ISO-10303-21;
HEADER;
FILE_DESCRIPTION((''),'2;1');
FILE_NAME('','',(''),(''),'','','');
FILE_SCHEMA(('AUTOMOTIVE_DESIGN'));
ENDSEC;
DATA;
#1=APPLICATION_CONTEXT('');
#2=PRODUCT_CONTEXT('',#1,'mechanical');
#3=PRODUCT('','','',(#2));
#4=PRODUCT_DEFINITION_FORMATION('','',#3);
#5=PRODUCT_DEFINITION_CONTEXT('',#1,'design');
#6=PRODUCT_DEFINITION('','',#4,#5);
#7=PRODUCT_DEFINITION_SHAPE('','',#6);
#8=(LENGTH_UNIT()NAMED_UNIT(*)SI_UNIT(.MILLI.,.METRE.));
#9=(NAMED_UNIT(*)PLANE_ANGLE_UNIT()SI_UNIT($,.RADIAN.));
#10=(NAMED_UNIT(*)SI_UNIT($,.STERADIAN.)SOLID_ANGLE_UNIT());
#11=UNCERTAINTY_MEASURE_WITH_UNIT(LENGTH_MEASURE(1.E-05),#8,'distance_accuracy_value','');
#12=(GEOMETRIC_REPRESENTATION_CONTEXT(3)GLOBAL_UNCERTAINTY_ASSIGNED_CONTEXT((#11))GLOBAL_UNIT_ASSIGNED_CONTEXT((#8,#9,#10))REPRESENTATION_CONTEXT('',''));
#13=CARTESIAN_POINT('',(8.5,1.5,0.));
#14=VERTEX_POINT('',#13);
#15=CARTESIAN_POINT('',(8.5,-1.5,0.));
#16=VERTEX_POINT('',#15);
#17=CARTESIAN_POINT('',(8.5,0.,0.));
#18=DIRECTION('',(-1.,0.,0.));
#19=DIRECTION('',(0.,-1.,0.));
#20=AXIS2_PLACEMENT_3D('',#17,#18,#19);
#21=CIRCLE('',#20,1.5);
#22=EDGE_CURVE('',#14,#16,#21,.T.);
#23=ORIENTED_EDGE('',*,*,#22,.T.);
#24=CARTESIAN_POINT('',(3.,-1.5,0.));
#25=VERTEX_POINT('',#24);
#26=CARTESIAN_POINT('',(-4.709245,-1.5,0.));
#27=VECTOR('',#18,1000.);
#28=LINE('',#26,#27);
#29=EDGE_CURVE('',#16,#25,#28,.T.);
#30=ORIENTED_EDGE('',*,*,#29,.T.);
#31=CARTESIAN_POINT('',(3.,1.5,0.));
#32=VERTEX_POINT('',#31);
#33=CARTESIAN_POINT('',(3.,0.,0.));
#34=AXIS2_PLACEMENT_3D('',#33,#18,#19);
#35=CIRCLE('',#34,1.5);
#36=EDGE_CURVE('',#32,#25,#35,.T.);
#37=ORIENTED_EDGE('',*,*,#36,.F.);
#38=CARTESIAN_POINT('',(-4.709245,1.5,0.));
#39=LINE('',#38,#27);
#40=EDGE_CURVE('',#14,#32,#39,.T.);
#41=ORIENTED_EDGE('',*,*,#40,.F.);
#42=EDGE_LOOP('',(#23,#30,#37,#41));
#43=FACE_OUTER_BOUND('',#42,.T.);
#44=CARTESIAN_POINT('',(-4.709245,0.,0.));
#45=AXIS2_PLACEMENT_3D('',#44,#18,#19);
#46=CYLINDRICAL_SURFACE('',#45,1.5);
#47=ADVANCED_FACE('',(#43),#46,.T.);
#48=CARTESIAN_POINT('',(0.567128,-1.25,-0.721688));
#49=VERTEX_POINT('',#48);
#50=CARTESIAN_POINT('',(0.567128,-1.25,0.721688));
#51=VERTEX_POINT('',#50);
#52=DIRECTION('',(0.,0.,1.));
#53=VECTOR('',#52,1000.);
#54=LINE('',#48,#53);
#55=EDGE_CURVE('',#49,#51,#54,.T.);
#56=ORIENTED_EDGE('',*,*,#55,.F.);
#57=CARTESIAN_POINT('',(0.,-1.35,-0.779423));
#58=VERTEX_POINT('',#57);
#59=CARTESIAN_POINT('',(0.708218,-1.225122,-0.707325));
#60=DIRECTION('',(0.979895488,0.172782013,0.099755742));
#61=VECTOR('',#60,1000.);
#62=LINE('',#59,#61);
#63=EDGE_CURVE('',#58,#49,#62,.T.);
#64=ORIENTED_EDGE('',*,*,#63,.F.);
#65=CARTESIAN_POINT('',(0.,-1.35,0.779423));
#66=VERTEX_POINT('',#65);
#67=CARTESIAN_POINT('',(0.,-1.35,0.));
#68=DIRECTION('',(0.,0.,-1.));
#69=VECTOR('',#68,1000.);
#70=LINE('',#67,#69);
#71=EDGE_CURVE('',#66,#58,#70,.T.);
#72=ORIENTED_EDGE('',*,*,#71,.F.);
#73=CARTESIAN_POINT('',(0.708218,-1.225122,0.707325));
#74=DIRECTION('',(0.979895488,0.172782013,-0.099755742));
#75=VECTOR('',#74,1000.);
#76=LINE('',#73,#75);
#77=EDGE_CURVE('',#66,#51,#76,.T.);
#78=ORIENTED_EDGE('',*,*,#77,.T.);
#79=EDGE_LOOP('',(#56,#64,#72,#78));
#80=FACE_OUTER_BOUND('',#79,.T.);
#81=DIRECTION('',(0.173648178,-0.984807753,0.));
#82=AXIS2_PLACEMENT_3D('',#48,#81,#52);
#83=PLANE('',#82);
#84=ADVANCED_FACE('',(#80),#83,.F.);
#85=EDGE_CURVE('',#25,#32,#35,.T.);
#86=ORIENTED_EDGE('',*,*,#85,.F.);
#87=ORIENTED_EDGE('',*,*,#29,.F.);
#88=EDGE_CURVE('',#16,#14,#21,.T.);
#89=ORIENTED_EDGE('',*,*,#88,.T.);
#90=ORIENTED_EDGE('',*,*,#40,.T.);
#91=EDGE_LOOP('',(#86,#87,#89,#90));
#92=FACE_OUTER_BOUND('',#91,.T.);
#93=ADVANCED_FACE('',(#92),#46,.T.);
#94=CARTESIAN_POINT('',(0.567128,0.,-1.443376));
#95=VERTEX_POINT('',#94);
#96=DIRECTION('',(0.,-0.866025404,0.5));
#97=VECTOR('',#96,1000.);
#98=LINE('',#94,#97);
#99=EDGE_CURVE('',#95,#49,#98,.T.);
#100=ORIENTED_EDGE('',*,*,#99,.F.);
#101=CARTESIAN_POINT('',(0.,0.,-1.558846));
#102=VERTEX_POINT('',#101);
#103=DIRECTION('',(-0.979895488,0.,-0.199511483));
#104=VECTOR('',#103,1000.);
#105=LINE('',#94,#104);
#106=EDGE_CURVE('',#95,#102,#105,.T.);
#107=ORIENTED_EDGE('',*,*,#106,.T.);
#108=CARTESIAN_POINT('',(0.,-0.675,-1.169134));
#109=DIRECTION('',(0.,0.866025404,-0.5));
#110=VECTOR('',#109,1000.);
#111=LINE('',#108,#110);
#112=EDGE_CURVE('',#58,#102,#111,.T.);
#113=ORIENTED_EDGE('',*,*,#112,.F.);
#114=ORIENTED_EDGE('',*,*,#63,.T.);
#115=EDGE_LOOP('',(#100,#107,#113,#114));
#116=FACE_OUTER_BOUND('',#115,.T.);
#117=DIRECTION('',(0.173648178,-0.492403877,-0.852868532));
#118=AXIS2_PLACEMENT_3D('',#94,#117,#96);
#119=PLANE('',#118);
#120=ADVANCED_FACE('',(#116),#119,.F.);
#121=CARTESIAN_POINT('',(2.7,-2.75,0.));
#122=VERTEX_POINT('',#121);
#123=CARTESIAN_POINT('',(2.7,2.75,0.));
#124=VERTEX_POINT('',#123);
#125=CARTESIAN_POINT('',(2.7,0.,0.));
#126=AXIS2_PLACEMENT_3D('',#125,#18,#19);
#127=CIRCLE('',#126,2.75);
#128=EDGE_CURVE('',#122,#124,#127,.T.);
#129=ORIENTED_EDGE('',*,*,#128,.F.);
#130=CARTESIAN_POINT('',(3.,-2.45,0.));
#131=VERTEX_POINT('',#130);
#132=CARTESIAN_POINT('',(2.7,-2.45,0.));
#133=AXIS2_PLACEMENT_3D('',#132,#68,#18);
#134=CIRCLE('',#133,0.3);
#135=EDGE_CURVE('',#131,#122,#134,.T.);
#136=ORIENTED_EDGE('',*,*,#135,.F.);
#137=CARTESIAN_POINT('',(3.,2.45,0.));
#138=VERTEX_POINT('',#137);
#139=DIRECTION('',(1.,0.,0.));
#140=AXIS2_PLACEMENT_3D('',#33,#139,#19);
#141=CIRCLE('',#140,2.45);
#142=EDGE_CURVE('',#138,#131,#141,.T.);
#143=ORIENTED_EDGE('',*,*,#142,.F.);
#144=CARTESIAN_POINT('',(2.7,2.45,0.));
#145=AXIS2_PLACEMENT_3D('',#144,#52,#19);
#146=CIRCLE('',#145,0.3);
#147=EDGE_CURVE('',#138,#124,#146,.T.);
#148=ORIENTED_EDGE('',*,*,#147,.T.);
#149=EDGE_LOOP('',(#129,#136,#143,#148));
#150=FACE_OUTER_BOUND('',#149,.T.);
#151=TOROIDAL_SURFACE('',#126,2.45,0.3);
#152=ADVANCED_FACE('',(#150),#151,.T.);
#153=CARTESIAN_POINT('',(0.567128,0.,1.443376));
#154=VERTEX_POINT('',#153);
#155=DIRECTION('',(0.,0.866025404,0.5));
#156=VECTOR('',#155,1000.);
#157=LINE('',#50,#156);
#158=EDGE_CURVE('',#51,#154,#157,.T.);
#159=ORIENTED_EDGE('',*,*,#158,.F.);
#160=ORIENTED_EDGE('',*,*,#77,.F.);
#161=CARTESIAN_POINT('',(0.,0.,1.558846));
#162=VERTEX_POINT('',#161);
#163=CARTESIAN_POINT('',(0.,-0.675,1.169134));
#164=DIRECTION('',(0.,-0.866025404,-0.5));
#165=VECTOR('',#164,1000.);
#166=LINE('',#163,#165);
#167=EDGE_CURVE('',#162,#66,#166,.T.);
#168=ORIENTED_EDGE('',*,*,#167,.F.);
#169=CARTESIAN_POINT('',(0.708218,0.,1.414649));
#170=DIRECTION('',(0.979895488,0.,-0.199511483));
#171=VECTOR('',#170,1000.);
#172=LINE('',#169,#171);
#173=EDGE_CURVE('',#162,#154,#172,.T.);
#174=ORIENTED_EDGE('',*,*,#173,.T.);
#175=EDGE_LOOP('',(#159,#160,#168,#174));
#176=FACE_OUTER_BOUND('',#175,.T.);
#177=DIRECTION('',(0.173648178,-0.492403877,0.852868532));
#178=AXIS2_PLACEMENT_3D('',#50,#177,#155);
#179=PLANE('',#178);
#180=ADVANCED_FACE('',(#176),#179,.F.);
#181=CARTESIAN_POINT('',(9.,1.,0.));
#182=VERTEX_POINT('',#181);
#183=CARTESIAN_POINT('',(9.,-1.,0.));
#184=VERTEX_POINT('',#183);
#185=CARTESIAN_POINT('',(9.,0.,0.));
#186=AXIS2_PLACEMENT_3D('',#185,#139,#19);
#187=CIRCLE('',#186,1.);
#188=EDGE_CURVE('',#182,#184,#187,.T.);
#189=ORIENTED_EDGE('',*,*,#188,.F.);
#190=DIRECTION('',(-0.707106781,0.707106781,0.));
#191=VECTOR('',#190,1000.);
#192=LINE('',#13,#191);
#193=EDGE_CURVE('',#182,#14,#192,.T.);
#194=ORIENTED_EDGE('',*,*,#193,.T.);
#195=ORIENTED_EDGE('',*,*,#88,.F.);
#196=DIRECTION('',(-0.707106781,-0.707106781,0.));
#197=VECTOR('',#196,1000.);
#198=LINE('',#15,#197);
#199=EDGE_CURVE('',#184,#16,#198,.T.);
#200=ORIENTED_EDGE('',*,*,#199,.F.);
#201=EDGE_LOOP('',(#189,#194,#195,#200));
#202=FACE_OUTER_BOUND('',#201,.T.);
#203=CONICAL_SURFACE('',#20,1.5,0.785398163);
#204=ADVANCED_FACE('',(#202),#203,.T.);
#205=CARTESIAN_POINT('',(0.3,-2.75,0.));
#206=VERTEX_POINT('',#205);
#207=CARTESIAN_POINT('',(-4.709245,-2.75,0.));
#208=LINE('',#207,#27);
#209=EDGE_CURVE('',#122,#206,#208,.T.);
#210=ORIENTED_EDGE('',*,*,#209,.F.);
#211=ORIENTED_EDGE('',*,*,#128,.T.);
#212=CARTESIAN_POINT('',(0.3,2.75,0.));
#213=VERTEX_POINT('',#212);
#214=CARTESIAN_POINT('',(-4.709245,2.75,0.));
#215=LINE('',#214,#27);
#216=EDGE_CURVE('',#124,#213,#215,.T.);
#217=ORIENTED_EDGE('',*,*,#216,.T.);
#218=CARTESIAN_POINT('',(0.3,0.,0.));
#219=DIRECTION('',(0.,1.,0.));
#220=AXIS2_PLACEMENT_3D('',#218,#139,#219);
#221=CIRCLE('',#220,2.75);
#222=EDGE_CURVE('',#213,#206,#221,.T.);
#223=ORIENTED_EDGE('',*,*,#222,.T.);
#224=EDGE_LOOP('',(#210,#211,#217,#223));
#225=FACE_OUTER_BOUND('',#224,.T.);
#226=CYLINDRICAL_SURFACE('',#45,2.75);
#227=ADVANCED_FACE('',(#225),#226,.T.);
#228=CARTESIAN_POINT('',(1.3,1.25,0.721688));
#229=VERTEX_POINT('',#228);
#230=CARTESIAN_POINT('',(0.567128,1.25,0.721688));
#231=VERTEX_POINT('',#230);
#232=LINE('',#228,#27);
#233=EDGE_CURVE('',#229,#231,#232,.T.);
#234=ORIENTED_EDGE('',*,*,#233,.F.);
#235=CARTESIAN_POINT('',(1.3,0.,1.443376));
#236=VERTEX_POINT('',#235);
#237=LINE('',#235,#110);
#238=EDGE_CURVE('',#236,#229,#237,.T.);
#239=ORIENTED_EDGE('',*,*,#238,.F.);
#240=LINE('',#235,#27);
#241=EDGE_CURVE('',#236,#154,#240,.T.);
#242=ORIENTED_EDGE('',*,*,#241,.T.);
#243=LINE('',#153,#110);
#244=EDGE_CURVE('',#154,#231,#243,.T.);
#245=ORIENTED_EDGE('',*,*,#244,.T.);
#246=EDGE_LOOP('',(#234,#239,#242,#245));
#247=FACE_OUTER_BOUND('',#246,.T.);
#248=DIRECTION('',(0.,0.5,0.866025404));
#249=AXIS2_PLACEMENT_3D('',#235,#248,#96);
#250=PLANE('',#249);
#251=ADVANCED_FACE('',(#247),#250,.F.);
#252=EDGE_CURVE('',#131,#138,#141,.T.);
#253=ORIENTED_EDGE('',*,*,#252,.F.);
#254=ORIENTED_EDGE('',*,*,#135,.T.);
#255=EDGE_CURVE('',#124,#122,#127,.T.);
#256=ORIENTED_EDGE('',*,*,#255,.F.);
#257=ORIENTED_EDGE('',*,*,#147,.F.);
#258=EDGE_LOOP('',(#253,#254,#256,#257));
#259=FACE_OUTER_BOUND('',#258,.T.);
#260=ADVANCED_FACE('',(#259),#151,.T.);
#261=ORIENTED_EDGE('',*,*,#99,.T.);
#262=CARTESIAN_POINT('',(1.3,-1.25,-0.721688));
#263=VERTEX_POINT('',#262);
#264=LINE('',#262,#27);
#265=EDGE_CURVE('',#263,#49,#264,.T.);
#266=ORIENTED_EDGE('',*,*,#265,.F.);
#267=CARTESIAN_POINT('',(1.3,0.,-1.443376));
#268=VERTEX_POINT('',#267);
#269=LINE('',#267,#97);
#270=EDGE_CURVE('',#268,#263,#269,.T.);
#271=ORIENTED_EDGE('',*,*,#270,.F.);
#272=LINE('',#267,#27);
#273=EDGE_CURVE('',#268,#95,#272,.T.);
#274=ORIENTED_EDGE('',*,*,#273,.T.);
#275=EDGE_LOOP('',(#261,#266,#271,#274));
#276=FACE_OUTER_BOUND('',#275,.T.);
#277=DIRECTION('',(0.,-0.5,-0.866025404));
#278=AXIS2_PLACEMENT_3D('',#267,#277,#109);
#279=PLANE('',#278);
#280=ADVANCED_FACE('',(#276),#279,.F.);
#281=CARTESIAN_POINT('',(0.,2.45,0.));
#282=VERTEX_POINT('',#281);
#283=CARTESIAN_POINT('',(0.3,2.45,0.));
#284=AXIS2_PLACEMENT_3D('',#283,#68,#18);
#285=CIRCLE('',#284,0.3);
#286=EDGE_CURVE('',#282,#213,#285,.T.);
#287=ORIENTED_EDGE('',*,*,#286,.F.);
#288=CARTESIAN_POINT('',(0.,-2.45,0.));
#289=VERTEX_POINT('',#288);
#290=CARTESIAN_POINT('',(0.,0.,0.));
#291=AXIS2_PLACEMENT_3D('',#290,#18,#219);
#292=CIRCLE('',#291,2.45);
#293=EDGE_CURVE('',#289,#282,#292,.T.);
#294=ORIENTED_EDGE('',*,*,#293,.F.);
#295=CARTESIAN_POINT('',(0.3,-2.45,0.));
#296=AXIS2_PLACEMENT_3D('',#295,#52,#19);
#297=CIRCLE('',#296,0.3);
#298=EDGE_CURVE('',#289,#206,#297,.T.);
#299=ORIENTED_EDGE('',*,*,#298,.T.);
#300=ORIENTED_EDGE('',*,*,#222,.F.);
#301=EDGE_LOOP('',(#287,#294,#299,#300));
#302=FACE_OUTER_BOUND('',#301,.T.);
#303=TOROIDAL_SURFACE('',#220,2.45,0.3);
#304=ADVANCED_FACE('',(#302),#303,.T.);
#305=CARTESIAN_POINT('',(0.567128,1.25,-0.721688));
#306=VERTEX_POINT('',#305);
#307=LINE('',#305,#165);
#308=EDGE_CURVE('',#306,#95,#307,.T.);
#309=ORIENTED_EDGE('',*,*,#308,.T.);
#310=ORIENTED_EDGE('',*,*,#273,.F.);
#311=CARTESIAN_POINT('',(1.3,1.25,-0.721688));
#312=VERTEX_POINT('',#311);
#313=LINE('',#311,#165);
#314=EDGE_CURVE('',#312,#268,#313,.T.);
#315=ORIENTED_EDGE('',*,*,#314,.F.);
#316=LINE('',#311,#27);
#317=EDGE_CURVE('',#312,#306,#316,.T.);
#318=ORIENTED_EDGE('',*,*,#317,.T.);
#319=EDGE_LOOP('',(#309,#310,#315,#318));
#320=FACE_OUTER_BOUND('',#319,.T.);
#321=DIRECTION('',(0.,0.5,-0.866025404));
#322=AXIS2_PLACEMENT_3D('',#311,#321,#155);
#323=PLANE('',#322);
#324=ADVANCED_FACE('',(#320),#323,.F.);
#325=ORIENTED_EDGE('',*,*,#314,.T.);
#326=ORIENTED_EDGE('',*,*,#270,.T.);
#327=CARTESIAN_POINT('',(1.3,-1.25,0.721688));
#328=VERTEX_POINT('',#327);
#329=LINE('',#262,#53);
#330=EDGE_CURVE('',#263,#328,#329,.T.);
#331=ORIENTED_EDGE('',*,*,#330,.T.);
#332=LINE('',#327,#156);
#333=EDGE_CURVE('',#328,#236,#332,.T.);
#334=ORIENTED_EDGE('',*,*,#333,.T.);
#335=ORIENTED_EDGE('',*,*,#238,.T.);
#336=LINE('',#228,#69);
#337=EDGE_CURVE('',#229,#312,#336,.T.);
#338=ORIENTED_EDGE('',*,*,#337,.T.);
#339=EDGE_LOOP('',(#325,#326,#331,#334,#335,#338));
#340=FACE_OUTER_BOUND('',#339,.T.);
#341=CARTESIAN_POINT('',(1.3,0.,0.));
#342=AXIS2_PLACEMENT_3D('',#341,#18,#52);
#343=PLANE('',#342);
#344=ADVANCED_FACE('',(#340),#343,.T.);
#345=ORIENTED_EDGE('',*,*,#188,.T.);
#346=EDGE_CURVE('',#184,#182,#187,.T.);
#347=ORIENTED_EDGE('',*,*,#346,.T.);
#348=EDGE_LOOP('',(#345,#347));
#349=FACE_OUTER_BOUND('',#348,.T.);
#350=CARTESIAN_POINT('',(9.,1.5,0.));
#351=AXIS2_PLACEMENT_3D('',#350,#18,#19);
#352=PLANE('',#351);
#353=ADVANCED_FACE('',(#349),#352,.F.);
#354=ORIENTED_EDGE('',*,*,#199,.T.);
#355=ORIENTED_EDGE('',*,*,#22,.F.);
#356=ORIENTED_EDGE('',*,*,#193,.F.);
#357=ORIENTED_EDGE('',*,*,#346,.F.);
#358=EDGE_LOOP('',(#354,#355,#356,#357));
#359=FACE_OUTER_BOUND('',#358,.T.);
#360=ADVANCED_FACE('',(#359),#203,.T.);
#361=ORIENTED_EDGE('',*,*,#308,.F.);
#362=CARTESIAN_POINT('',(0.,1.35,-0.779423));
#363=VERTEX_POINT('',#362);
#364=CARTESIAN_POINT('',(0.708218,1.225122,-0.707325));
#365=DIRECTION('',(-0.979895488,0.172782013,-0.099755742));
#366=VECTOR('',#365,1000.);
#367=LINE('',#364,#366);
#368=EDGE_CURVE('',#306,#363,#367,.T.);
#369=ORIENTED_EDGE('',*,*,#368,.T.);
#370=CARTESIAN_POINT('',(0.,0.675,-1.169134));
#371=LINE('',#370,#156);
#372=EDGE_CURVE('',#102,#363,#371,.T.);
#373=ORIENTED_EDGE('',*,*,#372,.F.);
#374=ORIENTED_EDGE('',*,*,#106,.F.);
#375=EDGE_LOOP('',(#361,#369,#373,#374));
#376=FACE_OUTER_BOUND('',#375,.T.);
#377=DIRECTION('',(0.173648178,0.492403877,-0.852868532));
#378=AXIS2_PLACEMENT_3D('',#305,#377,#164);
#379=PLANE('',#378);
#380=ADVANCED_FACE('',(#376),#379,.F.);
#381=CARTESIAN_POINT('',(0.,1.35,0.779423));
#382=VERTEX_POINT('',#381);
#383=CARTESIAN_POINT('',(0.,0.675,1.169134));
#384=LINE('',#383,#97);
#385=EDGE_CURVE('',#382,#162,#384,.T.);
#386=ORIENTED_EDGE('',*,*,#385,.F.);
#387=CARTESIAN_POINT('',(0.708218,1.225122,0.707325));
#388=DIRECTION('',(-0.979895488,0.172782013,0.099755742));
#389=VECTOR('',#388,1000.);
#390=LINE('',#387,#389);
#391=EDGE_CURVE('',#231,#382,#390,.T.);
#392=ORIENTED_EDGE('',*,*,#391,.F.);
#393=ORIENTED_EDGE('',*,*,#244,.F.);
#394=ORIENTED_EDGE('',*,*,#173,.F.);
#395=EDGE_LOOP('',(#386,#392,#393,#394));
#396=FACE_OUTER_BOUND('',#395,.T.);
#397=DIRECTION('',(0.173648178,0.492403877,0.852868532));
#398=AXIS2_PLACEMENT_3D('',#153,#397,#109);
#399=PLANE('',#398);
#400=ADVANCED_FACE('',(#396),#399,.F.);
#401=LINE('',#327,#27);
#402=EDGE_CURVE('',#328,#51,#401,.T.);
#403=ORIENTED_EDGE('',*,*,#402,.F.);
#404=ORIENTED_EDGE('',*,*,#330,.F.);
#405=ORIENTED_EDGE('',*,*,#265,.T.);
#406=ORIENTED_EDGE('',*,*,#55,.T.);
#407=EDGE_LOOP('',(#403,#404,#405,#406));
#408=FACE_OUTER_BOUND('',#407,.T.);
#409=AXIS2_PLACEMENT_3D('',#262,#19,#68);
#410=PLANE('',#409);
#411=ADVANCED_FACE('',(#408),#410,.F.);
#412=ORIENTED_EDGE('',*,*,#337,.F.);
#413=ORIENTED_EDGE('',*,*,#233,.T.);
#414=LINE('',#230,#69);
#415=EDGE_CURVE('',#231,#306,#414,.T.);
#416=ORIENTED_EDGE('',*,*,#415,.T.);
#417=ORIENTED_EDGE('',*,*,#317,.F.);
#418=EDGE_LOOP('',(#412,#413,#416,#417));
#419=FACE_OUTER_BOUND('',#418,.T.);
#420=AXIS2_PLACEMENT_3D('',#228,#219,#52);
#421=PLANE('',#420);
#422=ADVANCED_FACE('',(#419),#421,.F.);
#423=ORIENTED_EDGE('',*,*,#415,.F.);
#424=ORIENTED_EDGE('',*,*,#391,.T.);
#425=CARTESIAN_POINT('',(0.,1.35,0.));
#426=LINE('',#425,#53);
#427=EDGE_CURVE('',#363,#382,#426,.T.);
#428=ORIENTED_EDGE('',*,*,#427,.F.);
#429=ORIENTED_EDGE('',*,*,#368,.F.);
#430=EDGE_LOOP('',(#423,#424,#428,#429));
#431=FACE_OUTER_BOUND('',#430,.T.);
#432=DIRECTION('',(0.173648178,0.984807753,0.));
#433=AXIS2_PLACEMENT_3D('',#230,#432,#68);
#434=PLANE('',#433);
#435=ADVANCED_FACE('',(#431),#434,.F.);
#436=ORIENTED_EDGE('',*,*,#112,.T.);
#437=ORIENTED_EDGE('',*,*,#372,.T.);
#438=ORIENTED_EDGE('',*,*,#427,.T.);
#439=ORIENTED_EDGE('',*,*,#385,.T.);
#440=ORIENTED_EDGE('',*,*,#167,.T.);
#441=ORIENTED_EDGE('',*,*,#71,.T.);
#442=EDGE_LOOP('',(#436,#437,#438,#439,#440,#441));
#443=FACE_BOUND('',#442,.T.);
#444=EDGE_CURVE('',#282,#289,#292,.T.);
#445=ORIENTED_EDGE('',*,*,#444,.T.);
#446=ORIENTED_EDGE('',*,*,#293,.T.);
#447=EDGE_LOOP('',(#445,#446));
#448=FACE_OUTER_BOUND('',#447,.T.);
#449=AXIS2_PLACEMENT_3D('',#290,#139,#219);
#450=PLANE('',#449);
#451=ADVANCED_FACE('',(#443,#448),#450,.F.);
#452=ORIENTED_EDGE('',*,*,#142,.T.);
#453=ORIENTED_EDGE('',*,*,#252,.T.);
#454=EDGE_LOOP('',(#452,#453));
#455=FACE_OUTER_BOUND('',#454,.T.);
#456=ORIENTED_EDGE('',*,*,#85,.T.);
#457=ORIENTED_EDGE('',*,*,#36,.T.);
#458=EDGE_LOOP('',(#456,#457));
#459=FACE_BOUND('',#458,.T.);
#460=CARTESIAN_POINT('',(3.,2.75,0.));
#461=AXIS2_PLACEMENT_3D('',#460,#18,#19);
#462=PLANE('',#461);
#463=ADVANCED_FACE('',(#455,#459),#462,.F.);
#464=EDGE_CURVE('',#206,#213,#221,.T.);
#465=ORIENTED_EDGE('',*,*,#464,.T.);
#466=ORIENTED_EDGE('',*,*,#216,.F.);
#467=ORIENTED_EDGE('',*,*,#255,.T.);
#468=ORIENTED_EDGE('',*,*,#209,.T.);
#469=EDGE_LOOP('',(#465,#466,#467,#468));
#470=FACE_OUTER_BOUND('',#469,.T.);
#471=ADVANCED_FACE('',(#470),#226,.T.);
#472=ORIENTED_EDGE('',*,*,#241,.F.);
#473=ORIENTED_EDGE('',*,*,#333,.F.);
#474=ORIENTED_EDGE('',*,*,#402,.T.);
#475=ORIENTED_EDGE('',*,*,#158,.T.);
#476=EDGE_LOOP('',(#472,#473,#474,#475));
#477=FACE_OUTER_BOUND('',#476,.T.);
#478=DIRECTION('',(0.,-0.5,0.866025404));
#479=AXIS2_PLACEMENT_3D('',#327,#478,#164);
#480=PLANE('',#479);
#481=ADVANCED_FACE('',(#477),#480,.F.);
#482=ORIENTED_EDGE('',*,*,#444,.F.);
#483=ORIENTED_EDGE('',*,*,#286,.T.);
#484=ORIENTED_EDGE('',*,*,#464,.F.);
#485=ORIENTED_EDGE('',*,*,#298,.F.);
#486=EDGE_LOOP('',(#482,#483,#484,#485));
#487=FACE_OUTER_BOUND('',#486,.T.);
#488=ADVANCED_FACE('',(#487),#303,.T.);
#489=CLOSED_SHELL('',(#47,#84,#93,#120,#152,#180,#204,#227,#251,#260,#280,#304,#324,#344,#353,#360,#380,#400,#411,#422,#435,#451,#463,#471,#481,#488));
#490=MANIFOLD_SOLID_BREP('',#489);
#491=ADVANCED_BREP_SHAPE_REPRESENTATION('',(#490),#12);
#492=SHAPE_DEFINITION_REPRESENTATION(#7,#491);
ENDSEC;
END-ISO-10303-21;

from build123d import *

# Parameters (mm, degrees)
CUT_EXTRUDE1_DEPTH = 1.3
FILLET1_R          = 0.3
CHAMFER1_SIZE      = 0.1
CHAMFER1_SIZE2     = 0.567128182
CHAMFER2_SIZE      = 0.5


with BuildPart() as part:
    # Sketch1 → Revolve1 (revolve)
    with BuildSketch(Plane.XY, mode=Mode.PRIVATE) as revolve1_sk:
        Polygon((0, 0), (0, 2.75), (3, 2.75), (3, 1.5), (9, 1.5), (9, 0), align=None)
    revolve(revolve1_sk.sketch.rotate(Axis((-4.709244637, 0, 0), (1, 0, 0)), 180), axis=Axis((-4.709244637, 0, 0), (1, 0, 0)))

    # Sketch4 → Cut-Extrude1 (cut)
    with BuildSketch(Plane.ZY):
        Polygon((-1.443375673, 0), (-0.721687836, -1.25), (0.721687836, -1.25), (1.443375673, 0), (0.721687836, 1.25), (-0.721687836, 1.25), align=None)
    extrude(amount=-CUT_EXTRUDE1_DEPTH, mode=Mode.SUBTRACT)

    # Fillet1
    fillet1_edges = [part.edges().sort_by_distance(p)[0] for p in [
        (3, 2.75, 0),
        (0, 2.75, 0),
    ]]
    fillet(fillet1_edges, radius=FILLET1_R)

    # Chamfer1
    chamfer1_edges = [part.edges().sort_by_distance(p)[0] for p in [
        (0, 0.625, -1.082531755),
        (0, -0.625, -1.082531755),
        (0, -1.25, 0),
        (0, -0.625, 1.082531755),
        (0, 0.625, 1.082531755),
        (0, 1.25, 0),
    ]]
    chamfer1_side = [part.faces().sort_by_distance(p)[0] for p in [
        (0, 2.380703535, 0),
    ]]
    chamfer(chamfer1_edges, length=CHAMFER1_SIZE, length2=CHAMFER1_SIZE2, reference=chamfer1_side[0])

    # Chamfer2
    chamfer2_edges = [part.edges().sort_by_distance(p)[0] for p in [
        (9, 1.5, 0),
    ]]
    chamfer(chamfer2_edges, length=CHAMFER2_SIZE)


solid = part.part
